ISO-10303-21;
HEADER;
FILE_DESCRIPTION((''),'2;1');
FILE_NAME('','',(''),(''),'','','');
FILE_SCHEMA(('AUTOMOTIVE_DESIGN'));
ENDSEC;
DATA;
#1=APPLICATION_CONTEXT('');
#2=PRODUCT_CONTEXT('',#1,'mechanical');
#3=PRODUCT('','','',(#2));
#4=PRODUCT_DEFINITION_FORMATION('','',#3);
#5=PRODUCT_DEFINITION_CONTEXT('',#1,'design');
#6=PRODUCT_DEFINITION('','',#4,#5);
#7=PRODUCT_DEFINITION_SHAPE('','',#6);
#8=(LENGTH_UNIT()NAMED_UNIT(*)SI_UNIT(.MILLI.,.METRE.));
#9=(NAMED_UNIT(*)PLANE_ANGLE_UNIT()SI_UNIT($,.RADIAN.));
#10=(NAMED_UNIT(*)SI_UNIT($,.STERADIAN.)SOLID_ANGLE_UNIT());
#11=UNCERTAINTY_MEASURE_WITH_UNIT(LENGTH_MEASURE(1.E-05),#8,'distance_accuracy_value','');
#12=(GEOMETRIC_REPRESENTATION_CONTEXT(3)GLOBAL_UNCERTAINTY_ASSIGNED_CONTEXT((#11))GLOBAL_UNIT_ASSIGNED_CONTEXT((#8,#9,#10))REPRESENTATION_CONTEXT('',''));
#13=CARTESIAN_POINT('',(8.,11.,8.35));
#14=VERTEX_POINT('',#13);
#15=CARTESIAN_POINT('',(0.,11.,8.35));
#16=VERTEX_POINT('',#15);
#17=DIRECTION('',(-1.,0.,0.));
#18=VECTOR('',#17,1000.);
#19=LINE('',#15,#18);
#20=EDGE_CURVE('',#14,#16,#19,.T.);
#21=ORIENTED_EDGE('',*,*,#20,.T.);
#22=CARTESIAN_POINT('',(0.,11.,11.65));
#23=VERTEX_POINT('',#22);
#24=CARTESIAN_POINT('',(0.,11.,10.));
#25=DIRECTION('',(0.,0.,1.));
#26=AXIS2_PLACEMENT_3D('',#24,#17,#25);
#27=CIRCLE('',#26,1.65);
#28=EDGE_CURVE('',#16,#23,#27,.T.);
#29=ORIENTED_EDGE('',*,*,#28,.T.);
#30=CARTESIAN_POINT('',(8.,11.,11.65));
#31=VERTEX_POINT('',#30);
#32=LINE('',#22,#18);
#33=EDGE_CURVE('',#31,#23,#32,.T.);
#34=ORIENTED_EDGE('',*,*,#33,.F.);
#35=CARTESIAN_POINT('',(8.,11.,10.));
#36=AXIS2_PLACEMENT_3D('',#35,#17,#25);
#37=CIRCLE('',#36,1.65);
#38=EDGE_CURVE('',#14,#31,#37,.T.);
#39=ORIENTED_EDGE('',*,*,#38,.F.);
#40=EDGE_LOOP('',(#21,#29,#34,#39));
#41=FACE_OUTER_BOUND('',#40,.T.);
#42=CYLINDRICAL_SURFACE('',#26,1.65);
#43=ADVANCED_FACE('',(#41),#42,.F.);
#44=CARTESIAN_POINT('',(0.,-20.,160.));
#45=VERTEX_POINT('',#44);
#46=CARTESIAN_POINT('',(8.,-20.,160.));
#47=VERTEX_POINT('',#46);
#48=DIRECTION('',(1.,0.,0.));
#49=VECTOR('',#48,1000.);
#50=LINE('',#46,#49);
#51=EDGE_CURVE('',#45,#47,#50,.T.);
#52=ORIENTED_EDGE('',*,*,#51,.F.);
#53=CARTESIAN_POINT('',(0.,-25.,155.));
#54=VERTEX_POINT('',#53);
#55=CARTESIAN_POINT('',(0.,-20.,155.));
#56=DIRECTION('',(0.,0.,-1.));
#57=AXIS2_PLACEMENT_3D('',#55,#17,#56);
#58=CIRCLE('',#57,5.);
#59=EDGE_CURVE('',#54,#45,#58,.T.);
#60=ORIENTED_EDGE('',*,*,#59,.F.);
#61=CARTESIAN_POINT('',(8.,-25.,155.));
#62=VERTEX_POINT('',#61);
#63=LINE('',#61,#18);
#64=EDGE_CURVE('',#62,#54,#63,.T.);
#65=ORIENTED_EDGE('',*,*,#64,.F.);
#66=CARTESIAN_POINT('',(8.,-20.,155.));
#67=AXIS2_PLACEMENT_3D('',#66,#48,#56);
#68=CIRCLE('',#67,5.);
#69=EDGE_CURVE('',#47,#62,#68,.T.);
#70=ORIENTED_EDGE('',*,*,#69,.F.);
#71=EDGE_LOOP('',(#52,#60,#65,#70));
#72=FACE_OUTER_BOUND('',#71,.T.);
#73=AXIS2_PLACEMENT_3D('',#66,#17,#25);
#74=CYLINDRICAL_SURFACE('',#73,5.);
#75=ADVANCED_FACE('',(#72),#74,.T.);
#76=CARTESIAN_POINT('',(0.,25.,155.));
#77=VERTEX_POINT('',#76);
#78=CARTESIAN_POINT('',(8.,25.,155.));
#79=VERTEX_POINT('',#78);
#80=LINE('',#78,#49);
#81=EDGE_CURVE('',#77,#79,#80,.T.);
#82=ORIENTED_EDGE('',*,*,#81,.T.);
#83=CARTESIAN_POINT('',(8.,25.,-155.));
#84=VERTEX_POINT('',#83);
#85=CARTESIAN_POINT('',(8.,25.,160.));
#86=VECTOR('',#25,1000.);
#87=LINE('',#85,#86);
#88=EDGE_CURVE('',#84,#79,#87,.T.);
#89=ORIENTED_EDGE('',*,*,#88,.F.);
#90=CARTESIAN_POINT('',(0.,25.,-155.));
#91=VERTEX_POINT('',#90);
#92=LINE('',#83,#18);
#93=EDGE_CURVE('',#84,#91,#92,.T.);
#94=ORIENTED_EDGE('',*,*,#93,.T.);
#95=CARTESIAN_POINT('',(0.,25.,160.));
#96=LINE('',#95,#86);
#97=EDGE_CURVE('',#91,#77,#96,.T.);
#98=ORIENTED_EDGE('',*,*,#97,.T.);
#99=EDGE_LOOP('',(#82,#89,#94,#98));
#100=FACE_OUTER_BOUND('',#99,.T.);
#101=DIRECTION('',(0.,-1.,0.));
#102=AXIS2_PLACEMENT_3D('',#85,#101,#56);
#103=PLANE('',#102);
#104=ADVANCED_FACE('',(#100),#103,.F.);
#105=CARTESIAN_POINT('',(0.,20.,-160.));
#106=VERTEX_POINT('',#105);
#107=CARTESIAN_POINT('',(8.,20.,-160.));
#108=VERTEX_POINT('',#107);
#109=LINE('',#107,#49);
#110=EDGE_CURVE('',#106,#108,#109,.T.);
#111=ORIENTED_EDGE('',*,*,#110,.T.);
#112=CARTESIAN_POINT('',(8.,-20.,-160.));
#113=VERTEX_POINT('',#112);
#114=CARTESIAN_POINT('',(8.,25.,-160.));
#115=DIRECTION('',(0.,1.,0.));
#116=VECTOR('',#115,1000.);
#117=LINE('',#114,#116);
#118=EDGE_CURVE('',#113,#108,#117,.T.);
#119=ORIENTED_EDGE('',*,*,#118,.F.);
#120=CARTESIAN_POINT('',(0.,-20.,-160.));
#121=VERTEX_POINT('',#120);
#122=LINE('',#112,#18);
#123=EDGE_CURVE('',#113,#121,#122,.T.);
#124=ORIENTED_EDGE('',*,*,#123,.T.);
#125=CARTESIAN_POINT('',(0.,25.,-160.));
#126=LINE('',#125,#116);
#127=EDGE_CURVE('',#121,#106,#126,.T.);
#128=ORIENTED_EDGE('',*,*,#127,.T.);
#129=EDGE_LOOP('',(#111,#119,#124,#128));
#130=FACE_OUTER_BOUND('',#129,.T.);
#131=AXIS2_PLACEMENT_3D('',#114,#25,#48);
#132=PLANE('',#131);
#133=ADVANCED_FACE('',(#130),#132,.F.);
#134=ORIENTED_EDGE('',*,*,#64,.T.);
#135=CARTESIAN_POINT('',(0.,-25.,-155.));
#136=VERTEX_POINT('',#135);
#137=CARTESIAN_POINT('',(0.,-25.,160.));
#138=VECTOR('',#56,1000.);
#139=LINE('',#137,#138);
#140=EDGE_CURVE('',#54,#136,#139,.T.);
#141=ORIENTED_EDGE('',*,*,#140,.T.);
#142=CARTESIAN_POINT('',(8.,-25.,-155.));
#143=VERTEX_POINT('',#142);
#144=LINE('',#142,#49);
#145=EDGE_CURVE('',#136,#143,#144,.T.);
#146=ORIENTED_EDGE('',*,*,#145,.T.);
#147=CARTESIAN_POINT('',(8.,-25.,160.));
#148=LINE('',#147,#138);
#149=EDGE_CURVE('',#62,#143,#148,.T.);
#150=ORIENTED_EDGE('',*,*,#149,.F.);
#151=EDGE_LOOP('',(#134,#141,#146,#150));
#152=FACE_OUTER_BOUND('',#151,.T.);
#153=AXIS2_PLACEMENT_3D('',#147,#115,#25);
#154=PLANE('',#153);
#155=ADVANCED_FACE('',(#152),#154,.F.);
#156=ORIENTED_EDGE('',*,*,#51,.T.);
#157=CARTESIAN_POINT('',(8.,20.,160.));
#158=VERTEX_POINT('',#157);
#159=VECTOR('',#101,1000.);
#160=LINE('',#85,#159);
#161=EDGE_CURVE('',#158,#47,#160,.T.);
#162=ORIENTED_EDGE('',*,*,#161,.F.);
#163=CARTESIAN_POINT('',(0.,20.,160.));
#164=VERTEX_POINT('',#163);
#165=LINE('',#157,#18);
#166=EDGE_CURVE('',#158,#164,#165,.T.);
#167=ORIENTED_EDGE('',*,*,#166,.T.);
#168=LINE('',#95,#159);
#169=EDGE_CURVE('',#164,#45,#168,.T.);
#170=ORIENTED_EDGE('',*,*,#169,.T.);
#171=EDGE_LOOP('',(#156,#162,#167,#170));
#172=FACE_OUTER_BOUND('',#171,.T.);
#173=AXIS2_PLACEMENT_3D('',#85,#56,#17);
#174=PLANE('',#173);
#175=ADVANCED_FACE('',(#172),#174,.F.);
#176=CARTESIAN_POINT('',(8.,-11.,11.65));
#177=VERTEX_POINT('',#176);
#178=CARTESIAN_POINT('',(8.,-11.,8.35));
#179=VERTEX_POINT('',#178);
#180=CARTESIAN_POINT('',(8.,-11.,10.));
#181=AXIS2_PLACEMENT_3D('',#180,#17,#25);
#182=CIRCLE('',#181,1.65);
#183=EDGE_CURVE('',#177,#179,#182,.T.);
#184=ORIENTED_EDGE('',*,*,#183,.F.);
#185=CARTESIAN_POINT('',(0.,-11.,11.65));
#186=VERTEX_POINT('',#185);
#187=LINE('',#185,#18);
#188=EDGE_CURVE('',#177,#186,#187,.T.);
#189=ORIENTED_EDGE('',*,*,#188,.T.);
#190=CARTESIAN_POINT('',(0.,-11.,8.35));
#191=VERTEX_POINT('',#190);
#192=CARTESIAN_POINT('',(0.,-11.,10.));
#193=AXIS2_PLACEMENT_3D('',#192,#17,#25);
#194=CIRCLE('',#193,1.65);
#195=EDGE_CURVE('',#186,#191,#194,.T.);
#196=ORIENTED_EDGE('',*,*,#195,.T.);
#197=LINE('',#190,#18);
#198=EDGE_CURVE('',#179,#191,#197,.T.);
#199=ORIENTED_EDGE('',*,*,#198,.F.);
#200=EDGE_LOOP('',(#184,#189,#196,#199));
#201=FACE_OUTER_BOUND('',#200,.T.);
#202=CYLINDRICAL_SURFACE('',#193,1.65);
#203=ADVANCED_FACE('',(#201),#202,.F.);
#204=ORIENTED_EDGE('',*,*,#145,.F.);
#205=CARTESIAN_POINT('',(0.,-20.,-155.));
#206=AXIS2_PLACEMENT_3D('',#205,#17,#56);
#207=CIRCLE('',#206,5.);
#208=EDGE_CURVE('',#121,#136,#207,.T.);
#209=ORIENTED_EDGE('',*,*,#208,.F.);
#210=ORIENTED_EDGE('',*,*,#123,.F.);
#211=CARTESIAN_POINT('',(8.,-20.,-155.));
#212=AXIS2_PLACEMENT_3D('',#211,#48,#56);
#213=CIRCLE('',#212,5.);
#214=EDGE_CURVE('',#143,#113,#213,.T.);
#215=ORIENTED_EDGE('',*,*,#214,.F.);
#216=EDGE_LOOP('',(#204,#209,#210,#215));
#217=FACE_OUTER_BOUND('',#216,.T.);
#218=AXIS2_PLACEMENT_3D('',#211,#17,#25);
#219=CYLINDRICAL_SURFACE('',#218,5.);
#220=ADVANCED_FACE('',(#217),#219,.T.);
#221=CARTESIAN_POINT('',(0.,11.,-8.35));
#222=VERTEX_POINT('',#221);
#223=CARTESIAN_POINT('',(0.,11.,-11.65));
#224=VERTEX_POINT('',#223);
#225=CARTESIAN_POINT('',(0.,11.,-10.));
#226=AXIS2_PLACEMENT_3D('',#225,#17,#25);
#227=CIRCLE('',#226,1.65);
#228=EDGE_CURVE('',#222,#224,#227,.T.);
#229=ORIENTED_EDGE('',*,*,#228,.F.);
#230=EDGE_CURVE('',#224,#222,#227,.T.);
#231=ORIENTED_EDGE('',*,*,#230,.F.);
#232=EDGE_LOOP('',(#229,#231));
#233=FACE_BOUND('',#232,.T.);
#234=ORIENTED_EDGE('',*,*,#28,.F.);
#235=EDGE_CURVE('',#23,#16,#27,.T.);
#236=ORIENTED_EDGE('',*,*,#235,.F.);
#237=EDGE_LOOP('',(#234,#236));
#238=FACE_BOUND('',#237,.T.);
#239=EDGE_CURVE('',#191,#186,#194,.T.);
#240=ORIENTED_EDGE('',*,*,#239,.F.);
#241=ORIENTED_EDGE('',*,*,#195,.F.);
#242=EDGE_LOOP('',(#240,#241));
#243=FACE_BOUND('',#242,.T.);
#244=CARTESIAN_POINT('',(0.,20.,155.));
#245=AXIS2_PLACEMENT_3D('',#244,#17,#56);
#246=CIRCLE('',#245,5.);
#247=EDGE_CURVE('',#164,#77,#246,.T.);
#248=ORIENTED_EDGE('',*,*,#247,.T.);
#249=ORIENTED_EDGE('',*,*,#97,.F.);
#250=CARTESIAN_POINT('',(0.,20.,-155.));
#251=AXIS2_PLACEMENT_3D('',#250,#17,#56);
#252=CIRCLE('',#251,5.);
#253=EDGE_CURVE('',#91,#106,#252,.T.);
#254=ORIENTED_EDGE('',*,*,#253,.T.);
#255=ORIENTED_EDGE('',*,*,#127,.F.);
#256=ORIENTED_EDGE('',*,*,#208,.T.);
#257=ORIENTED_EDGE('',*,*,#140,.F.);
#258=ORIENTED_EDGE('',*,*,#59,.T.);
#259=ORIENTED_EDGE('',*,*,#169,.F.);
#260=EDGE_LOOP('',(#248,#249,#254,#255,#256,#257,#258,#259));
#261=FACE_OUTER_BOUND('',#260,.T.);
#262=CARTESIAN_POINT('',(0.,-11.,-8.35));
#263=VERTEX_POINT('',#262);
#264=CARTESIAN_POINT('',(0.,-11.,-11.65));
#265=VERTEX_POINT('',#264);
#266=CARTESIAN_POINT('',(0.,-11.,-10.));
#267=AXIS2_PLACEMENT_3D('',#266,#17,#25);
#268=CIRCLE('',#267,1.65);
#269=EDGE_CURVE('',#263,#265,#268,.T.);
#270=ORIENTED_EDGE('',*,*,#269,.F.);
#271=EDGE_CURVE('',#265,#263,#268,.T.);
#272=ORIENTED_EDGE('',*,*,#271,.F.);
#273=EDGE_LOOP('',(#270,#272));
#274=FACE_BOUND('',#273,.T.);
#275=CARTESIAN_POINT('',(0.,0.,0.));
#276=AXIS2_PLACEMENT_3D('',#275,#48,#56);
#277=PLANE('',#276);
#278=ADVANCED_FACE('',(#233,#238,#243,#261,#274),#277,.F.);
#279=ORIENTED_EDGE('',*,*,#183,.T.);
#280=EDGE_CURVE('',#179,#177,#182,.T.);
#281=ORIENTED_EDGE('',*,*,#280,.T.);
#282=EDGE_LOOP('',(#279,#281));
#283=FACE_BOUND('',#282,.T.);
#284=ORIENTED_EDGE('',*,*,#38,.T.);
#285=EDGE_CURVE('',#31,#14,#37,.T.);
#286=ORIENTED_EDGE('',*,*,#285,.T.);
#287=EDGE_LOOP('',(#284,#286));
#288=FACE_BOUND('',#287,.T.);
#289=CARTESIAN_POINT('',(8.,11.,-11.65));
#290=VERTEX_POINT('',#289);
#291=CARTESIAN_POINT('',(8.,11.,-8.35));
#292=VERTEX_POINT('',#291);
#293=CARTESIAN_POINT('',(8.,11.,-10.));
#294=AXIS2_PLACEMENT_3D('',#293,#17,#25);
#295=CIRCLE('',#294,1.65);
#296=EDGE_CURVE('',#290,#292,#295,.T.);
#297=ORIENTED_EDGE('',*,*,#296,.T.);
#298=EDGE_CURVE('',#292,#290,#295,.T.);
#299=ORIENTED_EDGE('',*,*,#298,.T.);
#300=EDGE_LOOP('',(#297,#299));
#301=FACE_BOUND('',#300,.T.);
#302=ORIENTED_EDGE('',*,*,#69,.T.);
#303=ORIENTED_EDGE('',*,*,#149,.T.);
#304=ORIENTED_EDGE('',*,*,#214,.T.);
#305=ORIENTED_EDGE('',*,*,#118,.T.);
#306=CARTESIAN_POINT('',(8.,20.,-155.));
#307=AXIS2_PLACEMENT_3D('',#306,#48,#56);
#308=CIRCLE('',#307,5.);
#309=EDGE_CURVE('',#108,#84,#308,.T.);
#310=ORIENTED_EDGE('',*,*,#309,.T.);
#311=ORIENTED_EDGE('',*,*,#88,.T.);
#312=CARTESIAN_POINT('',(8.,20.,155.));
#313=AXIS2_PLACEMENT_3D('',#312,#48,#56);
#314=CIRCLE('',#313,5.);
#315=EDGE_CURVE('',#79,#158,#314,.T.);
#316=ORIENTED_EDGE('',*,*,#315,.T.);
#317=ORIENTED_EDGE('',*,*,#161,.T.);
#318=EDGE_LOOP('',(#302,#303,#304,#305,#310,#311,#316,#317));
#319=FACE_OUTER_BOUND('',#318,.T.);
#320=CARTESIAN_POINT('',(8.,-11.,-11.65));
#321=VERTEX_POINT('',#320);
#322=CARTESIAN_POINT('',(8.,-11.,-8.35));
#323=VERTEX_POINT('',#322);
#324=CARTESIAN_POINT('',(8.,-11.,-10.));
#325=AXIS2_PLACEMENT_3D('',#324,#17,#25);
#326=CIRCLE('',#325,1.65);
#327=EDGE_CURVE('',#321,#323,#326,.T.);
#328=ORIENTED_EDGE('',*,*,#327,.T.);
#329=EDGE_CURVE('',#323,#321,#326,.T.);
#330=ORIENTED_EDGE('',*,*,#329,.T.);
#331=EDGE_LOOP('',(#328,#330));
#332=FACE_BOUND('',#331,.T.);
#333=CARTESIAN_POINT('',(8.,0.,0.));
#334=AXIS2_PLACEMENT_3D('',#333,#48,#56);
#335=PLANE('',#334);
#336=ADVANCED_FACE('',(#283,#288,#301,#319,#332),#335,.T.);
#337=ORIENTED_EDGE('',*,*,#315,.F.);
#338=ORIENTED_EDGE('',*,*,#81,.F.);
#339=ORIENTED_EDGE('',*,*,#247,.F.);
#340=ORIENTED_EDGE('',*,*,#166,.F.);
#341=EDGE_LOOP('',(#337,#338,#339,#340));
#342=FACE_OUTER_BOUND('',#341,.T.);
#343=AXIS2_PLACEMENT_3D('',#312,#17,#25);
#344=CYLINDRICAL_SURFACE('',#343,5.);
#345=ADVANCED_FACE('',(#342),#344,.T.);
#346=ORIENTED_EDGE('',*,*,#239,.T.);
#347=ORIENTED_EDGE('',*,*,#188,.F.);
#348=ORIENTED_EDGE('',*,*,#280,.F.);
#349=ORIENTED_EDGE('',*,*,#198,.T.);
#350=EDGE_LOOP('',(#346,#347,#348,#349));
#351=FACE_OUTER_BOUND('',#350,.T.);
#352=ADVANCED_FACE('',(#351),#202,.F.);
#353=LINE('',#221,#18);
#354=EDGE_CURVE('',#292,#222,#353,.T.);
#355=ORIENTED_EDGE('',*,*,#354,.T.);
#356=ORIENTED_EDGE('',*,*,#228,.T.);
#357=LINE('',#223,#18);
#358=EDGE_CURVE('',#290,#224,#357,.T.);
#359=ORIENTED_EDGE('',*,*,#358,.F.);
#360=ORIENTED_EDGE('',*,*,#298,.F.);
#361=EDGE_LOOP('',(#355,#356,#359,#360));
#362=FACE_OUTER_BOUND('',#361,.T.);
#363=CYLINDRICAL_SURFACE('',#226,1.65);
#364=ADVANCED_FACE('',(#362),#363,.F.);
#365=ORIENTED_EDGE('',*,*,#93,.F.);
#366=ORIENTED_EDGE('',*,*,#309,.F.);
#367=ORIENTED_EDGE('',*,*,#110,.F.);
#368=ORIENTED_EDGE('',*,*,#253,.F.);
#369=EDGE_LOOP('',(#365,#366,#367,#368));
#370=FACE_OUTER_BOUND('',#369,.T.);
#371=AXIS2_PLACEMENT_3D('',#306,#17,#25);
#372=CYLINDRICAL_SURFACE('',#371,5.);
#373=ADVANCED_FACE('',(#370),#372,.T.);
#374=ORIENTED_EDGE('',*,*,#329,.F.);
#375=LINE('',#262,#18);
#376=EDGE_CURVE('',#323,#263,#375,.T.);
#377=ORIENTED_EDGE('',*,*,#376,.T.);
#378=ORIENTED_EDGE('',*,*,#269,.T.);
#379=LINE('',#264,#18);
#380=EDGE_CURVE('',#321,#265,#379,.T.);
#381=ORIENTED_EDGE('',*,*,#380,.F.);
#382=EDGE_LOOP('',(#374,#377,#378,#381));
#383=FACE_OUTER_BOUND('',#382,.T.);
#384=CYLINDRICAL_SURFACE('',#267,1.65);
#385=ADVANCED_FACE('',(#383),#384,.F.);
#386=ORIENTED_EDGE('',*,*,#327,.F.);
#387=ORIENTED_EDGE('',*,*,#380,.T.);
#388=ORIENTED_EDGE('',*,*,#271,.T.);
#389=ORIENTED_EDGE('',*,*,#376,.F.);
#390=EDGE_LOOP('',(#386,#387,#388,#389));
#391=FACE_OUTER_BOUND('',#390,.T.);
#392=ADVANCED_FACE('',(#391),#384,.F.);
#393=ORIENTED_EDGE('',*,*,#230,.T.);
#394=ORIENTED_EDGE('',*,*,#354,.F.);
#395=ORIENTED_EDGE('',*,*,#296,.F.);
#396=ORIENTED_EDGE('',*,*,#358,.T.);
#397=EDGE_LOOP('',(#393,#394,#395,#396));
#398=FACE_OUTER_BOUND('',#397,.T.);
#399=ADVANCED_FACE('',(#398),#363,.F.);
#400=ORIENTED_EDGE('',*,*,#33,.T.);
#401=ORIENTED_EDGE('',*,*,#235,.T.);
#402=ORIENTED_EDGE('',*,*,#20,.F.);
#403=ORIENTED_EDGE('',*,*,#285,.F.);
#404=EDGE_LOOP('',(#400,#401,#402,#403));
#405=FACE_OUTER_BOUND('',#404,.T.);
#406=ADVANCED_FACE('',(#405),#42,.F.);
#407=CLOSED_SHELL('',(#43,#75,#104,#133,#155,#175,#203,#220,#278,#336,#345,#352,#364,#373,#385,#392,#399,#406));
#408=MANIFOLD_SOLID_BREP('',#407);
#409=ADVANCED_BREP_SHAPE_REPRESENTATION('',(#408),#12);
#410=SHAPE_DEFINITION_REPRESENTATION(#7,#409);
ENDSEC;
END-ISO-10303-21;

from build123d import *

# Parameters (mm, degrees)
SKETCH_1_W         = 320
SKETCH_1_H         = 50
EXTRUDE_1_DEPTH    = 8
HOLE_WIZARD_M4_1_D = 3.3
FILLET_1_R         = 5


with BuildPart() as part:
    # 草图1 → 凸台-拉伸1 (new body)
    with BuildSketch(Plane(origin=(0, 0, 0), x_dir=(0, 0, -1), z_dir=(1, 0, 0))):
        Rectangle(SKETCH_1_W, SKETCH_1_H)
    extrude(amount=EXTRUDE_1_DEPTH)

    # M4 螺纹孔1 (through all)
    with Locations(Plane.ZY):
        with Locations((-10, -11), (-10, 11), (10, -11), (10, 11)):
            Hole(HOLE_WIZARD_M4_1_D / 2)

    # 圆角1
    fillet_1_edges = [part.edges().sort_by_distance(p)[0] for p in [
        (4, -25, -160),
        (4, -25, 160),
        (4, 25, 160),
        (4, 25, -160),
    ]]
    fillet(fillet_1_edges, radius=FILLET_1_R)


solid = part.part
